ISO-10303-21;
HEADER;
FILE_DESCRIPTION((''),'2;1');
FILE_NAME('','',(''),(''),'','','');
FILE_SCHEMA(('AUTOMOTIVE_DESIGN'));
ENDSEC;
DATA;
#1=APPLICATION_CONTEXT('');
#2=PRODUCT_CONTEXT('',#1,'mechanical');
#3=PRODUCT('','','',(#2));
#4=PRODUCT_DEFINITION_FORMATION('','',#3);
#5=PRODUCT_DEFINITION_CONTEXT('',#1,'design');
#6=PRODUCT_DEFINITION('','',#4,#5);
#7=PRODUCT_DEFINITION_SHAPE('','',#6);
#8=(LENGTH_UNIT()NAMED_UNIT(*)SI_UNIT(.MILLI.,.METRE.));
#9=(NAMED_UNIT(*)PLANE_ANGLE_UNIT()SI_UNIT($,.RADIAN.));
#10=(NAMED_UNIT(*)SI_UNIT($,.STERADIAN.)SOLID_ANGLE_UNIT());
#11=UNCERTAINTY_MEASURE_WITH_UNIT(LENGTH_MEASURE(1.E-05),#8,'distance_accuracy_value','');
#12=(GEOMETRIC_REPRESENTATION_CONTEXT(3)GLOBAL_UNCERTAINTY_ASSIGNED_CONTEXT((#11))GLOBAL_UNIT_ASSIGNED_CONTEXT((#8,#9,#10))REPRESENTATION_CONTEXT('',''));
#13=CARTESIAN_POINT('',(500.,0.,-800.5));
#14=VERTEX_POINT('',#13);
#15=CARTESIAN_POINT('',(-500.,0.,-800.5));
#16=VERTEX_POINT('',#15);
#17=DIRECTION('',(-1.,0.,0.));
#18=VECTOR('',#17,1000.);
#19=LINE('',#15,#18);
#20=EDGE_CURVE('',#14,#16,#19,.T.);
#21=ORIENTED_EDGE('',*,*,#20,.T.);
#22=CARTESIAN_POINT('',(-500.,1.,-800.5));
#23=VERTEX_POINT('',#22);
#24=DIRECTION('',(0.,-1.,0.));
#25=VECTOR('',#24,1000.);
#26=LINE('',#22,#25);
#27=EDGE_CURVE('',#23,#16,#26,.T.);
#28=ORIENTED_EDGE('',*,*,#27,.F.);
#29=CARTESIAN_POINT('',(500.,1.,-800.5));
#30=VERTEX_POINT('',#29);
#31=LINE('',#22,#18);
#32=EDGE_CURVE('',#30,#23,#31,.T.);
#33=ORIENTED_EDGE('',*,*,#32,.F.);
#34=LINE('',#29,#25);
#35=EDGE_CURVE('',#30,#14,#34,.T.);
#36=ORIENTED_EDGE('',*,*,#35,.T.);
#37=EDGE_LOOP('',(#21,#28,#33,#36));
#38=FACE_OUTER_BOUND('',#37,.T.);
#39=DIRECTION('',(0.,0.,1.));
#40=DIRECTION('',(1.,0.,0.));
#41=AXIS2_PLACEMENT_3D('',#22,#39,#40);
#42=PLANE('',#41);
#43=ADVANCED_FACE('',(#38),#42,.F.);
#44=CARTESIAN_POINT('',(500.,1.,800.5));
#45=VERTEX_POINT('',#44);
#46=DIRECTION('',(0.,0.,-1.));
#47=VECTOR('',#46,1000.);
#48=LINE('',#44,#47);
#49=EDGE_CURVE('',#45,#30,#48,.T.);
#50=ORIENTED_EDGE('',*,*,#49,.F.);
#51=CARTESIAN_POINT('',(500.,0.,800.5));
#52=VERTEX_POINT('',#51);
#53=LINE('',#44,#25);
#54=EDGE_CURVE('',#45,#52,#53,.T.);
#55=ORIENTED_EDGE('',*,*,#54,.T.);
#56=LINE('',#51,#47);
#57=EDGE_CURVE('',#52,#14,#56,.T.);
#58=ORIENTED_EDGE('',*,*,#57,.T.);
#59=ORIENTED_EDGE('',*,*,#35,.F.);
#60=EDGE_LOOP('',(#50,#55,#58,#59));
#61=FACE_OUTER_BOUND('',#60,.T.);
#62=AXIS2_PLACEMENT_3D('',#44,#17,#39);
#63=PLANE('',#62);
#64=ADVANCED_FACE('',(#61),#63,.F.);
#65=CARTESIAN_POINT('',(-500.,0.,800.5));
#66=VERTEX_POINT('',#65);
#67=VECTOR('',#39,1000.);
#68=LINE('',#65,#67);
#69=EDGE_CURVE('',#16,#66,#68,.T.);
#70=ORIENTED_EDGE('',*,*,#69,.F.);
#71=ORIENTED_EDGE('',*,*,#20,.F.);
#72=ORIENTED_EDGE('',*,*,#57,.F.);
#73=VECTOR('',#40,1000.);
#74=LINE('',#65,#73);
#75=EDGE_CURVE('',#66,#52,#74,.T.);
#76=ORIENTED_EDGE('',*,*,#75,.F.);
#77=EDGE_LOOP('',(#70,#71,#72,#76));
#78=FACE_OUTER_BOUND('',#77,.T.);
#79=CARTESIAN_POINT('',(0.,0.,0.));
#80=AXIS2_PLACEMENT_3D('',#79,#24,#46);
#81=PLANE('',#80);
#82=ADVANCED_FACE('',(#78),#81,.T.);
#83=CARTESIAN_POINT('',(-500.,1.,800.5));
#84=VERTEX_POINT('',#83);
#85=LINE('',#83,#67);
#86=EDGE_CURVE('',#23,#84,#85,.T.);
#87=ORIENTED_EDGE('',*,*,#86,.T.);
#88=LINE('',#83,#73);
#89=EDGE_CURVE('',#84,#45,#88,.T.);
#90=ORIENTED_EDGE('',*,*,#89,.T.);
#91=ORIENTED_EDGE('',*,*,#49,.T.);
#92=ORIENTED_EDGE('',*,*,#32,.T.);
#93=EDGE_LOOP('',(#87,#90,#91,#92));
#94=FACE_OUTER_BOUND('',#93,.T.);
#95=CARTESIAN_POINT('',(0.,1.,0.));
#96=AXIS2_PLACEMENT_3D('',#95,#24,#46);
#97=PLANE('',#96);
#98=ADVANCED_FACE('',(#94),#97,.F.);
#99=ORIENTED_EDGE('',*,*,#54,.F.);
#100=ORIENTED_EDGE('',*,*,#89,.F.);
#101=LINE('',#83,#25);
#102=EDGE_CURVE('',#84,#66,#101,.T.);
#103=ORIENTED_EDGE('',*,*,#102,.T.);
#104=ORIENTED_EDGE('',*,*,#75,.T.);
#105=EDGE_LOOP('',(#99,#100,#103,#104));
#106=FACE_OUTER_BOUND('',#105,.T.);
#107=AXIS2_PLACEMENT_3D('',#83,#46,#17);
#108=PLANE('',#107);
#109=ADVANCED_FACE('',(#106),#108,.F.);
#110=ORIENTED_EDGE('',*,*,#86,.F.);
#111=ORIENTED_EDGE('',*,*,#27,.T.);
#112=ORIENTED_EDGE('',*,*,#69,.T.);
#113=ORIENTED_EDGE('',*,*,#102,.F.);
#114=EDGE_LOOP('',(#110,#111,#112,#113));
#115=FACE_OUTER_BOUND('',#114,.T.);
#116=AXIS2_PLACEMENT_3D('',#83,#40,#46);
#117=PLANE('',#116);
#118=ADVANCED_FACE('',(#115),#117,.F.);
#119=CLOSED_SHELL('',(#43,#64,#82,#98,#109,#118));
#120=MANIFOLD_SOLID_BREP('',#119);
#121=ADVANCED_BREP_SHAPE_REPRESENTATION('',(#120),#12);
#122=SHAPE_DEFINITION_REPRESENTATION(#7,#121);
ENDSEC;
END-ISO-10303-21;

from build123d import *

# Parameters (mm, degrees)
SKETCH1_W           = 1000
SKETCH1_H           = 1601
BOSS_EXTRUDE1_DEPTH = 1


with BuildPart() as part:
    # Sketch1 → Boss-Extrude1 (new body)
    with BuildSketch(Plane(origin=(0, 0, 0), x_dir=(1, 0, 0), z_dir=(0, 1, 0))):
        Rectangle(SKETCH1_W, SKETCH1_H)
    extrude(amount=BOSS_EXTRUDE1_DEPTH)


solid = part.part
